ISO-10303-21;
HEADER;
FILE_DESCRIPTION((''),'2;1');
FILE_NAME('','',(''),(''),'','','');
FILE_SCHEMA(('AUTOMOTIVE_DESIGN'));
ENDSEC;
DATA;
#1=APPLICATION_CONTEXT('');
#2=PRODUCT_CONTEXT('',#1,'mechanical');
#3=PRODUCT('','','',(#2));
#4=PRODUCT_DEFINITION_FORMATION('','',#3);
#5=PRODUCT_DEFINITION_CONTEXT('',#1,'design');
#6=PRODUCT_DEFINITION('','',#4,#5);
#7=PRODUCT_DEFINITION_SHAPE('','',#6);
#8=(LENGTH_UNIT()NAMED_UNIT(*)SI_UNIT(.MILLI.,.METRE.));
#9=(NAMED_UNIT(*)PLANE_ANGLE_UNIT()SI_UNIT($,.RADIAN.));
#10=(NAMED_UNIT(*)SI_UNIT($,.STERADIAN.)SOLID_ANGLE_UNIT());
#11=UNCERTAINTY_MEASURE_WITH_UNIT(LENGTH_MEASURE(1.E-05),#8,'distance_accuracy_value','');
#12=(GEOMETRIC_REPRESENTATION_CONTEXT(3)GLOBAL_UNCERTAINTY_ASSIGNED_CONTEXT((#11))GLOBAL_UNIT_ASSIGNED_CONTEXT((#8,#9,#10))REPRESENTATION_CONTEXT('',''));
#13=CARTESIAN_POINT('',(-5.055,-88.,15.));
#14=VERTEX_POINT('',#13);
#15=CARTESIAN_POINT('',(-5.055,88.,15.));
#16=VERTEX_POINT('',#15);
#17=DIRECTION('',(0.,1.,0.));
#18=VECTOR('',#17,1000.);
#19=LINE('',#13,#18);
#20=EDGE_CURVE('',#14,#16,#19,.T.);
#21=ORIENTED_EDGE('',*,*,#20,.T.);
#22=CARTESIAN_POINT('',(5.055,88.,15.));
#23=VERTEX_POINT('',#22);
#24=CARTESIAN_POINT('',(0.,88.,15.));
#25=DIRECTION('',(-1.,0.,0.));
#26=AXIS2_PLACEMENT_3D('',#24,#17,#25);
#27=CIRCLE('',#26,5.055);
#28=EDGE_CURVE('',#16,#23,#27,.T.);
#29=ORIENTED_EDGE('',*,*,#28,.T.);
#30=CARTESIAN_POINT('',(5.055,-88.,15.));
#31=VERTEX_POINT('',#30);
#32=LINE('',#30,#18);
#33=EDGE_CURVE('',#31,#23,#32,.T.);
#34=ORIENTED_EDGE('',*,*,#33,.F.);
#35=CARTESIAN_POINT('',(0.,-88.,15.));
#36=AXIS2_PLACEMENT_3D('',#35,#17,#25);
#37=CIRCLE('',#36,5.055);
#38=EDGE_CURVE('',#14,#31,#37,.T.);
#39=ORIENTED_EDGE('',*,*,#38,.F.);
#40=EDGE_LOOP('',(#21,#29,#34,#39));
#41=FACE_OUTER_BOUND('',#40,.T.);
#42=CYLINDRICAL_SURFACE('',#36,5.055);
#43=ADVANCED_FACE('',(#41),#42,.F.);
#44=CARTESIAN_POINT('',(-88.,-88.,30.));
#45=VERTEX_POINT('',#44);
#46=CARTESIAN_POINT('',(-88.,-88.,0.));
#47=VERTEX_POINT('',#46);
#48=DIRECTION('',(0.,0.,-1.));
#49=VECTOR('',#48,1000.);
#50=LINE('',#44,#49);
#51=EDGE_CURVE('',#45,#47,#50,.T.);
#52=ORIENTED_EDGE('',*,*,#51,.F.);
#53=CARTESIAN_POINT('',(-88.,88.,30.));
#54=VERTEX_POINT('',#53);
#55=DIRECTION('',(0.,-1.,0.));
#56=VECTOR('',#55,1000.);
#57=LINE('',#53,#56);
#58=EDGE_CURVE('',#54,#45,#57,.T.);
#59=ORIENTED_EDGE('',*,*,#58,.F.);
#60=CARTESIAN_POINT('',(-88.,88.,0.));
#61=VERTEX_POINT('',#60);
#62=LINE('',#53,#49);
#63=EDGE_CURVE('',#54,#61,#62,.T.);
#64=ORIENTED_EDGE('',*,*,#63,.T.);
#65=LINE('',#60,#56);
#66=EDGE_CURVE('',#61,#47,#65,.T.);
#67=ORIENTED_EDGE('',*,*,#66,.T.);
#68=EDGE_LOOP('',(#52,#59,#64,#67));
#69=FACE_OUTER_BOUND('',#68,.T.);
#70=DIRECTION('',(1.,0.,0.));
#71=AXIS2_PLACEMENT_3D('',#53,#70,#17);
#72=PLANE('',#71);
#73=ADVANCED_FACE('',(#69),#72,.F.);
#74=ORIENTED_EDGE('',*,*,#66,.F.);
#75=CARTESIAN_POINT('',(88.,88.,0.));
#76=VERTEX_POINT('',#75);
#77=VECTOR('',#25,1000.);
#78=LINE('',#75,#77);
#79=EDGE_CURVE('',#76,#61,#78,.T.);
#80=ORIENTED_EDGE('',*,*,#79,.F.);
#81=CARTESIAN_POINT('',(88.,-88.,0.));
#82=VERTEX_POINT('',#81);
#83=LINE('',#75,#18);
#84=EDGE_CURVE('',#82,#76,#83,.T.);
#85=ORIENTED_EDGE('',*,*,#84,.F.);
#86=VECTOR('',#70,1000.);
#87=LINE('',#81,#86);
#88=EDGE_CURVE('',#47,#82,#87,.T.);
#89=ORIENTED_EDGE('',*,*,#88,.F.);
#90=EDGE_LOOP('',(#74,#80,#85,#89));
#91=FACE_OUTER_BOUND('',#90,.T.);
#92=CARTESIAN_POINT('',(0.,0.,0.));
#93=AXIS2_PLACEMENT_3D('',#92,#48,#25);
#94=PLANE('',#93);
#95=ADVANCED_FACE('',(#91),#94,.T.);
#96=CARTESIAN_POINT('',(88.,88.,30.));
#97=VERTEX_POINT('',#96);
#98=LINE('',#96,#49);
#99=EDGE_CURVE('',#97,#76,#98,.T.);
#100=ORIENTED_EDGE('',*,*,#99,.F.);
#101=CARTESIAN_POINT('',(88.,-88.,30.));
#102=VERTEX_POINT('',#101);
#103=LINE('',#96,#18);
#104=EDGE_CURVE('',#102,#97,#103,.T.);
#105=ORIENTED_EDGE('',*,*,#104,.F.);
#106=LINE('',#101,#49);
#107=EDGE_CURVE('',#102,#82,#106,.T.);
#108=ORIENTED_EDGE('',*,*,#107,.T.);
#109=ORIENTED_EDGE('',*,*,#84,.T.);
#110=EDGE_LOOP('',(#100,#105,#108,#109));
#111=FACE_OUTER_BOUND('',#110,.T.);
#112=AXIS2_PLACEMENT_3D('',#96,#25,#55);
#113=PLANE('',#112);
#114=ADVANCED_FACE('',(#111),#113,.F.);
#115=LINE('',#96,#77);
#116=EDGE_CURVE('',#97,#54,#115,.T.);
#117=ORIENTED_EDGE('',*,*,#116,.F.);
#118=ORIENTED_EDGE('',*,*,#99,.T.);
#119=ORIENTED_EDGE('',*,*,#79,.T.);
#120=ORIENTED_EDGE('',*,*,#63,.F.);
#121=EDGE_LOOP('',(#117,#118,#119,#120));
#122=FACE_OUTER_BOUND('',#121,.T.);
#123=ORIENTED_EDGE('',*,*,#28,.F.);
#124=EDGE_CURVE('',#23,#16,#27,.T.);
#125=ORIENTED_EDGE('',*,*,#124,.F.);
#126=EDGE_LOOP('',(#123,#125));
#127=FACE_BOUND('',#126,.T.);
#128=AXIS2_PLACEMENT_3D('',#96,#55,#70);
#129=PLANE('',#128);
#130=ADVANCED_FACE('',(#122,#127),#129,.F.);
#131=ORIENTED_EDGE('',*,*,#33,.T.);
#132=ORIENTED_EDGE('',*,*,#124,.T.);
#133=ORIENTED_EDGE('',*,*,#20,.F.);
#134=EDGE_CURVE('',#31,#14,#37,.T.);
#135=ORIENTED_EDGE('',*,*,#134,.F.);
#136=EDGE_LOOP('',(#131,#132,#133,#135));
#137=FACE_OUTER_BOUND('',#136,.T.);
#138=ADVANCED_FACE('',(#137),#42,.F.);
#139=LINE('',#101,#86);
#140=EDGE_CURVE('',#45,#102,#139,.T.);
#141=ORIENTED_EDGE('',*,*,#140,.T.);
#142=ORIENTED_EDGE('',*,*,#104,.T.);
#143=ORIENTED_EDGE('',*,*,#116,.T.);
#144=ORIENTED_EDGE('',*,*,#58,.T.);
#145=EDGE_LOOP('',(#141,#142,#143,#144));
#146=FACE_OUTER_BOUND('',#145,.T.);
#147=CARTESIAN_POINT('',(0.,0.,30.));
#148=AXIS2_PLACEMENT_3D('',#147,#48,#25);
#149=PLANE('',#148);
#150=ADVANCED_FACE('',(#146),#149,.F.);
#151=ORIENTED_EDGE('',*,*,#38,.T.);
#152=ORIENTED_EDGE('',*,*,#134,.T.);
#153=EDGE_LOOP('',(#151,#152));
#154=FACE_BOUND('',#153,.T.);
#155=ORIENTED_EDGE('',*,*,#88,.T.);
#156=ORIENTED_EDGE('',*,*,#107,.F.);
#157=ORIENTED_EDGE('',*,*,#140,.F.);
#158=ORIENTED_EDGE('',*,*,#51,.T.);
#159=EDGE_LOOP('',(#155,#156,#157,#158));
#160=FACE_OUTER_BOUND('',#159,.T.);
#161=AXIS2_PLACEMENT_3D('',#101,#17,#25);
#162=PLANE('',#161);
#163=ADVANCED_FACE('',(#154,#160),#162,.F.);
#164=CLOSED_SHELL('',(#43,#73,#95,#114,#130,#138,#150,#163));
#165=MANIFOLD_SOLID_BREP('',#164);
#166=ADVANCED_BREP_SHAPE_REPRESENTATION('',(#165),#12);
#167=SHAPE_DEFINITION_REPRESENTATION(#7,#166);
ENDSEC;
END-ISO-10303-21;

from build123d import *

# Parameters (mm, degrees)
SKETCH1_W           = 176
SKETCH1_H           = 176
BOSS_EXTRUDE1_DEPTH = 30
SKETCH3_R           = 5.055
CUT_EXTRUDE1_DEPTH  = 200.047732969


with BuildPart() as part:
    # Sketch1 → Boss-Extrude1 (new body)
    with BuildSketch(Plane.XY):
        Rectangle(SKETCH1_W, SKETCH1_H)
    extrude(amount=BOSS_EXTRUDE1_DEPTH)

    # Sketch3 → Cut-Extrude1 (cut, through all)
    with BuildSketch(Plane(origin=(0, 88, 0), x_dir=(1, 0, 0), z_dir=(0, 1, 0))):
        with Locations(Location((0, -15, 0), (0, 0, 180))):
            Circle(SKETCH3_R)
    extrude(amount=-CUT_EXTRUDE1_DEPTH, mode=Mode.SUBTRACT)


solid = part.part
